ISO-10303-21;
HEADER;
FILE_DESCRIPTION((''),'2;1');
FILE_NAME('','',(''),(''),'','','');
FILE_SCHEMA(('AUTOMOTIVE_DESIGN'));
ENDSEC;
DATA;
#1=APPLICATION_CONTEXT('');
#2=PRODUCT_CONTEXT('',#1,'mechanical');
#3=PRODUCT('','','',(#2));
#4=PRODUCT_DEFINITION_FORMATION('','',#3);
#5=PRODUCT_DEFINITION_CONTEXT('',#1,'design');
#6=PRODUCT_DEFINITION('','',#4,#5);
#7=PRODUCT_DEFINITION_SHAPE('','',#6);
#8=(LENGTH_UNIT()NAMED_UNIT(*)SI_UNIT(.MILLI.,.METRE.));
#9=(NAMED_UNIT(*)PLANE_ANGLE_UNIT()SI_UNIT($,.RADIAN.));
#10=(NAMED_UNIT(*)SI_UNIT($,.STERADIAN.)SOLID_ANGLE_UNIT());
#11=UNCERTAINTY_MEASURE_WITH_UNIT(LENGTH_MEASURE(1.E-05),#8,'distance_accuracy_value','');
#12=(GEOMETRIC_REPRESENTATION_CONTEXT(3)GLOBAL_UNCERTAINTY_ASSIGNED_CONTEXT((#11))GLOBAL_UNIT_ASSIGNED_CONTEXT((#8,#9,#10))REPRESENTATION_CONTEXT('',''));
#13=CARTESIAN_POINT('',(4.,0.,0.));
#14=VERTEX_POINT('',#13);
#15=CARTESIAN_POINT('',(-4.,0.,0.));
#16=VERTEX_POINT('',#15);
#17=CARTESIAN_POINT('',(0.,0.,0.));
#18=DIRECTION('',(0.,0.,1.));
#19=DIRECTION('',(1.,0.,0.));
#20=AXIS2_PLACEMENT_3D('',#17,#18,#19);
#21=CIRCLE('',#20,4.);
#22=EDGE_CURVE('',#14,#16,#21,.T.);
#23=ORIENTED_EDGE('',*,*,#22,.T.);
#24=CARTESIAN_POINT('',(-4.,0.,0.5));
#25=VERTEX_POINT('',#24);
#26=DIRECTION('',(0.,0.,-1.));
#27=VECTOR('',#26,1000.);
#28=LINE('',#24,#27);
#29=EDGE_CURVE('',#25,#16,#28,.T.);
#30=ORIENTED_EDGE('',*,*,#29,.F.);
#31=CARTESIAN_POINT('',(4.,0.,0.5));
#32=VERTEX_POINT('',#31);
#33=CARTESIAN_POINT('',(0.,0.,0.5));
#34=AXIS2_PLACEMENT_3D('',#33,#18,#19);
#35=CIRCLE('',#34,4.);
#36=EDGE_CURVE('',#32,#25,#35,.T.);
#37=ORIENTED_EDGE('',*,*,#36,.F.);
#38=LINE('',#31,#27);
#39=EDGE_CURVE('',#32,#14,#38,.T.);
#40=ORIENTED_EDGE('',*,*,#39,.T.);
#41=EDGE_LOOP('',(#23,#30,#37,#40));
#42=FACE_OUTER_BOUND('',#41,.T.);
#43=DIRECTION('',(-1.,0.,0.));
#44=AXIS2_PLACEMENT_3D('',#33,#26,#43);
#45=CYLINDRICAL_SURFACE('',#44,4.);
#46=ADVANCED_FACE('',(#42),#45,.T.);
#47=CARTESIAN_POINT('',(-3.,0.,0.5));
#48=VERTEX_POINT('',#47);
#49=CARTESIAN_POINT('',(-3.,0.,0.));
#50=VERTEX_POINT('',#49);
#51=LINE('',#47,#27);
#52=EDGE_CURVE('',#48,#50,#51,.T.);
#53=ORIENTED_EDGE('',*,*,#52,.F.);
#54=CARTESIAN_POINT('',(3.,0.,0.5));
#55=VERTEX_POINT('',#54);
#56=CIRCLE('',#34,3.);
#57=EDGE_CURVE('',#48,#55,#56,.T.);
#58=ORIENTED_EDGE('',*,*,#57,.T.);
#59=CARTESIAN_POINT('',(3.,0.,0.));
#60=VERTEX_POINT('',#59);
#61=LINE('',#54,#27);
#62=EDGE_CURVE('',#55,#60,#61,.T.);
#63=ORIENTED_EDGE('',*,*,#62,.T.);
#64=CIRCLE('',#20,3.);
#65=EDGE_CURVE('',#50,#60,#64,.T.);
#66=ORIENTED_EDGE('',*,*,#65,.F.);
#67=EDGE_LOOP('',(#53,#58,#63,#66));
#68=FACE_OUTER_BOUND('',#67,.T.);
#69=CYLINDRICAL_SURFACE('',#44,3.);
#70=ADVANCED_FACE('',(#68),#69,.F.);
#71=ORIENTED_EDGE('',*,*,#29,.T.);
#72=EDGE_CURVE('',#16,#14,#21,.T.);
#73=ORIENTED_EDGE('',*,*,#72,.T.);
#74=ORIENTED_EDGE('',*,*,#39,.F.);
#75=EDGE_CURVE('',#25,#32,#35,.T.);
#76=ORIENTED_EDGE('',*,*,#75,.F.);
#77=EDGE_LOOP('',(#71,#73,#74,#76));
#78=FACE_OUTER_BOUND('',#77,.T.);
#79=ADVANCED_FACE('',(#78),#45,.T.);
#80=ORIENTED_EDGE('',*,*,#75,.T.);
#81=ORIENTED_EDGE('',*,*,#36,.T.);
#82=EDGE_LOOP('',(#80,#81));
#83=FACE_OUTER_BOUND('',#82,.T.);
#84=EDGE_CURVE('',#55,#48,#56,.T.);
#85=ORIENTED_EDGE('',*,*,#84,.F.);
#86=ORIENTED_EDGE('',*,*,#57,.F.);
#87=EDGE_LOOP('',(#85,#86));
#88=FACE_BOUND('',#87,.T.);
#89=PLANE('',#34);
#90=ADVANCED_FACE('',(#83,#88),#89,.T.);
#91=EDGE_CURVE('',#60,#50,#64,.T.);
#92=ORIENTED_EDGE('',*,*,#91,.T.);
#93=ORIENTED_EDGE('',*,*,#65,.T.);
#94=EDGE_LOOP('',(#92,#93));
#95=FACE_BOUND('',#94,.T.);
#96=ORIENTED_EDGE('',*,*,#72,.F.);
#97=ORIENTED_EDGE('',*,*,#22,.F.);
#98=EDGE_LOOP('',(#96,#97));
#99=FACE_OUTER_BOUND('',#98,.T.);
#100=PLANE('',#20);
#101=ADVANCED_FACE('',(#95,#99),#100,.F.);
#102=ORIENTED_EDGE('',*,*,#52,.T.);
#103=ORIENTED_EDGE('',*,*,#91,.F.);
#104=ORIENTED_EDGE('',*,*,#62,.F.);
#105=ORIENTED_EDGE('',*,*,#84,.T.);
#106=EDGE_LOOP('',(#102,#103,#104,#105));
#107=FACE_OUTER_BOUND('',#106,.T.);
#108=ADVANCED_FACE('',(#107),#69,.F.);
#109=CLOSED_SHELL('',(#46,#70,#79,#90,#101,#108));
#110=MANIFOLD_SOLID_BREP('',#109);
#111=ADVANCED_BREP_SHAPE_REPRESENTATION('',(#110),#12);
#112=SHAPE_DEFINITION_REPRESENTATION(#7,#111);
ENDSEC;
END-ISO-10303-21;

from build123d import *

# Parameters (mm, degrees)
SKETCH_1_R      = 4
SKETCH_1_R_2    = 3
EXTRUDE_1_DEPTH = 0.5


with BuildPart() as part:
    # 草图1 → 凸台-拉伸1 (new body)
    with BuildSketch(Plane.XY):
        Circle(SKETCH_1_R)
        Circle(SKETCH_1_R_2, mode=Mode.SUBTRACT)
    extrude(amount=EXTRUDE_1_DEPTH)


solid = part.part
